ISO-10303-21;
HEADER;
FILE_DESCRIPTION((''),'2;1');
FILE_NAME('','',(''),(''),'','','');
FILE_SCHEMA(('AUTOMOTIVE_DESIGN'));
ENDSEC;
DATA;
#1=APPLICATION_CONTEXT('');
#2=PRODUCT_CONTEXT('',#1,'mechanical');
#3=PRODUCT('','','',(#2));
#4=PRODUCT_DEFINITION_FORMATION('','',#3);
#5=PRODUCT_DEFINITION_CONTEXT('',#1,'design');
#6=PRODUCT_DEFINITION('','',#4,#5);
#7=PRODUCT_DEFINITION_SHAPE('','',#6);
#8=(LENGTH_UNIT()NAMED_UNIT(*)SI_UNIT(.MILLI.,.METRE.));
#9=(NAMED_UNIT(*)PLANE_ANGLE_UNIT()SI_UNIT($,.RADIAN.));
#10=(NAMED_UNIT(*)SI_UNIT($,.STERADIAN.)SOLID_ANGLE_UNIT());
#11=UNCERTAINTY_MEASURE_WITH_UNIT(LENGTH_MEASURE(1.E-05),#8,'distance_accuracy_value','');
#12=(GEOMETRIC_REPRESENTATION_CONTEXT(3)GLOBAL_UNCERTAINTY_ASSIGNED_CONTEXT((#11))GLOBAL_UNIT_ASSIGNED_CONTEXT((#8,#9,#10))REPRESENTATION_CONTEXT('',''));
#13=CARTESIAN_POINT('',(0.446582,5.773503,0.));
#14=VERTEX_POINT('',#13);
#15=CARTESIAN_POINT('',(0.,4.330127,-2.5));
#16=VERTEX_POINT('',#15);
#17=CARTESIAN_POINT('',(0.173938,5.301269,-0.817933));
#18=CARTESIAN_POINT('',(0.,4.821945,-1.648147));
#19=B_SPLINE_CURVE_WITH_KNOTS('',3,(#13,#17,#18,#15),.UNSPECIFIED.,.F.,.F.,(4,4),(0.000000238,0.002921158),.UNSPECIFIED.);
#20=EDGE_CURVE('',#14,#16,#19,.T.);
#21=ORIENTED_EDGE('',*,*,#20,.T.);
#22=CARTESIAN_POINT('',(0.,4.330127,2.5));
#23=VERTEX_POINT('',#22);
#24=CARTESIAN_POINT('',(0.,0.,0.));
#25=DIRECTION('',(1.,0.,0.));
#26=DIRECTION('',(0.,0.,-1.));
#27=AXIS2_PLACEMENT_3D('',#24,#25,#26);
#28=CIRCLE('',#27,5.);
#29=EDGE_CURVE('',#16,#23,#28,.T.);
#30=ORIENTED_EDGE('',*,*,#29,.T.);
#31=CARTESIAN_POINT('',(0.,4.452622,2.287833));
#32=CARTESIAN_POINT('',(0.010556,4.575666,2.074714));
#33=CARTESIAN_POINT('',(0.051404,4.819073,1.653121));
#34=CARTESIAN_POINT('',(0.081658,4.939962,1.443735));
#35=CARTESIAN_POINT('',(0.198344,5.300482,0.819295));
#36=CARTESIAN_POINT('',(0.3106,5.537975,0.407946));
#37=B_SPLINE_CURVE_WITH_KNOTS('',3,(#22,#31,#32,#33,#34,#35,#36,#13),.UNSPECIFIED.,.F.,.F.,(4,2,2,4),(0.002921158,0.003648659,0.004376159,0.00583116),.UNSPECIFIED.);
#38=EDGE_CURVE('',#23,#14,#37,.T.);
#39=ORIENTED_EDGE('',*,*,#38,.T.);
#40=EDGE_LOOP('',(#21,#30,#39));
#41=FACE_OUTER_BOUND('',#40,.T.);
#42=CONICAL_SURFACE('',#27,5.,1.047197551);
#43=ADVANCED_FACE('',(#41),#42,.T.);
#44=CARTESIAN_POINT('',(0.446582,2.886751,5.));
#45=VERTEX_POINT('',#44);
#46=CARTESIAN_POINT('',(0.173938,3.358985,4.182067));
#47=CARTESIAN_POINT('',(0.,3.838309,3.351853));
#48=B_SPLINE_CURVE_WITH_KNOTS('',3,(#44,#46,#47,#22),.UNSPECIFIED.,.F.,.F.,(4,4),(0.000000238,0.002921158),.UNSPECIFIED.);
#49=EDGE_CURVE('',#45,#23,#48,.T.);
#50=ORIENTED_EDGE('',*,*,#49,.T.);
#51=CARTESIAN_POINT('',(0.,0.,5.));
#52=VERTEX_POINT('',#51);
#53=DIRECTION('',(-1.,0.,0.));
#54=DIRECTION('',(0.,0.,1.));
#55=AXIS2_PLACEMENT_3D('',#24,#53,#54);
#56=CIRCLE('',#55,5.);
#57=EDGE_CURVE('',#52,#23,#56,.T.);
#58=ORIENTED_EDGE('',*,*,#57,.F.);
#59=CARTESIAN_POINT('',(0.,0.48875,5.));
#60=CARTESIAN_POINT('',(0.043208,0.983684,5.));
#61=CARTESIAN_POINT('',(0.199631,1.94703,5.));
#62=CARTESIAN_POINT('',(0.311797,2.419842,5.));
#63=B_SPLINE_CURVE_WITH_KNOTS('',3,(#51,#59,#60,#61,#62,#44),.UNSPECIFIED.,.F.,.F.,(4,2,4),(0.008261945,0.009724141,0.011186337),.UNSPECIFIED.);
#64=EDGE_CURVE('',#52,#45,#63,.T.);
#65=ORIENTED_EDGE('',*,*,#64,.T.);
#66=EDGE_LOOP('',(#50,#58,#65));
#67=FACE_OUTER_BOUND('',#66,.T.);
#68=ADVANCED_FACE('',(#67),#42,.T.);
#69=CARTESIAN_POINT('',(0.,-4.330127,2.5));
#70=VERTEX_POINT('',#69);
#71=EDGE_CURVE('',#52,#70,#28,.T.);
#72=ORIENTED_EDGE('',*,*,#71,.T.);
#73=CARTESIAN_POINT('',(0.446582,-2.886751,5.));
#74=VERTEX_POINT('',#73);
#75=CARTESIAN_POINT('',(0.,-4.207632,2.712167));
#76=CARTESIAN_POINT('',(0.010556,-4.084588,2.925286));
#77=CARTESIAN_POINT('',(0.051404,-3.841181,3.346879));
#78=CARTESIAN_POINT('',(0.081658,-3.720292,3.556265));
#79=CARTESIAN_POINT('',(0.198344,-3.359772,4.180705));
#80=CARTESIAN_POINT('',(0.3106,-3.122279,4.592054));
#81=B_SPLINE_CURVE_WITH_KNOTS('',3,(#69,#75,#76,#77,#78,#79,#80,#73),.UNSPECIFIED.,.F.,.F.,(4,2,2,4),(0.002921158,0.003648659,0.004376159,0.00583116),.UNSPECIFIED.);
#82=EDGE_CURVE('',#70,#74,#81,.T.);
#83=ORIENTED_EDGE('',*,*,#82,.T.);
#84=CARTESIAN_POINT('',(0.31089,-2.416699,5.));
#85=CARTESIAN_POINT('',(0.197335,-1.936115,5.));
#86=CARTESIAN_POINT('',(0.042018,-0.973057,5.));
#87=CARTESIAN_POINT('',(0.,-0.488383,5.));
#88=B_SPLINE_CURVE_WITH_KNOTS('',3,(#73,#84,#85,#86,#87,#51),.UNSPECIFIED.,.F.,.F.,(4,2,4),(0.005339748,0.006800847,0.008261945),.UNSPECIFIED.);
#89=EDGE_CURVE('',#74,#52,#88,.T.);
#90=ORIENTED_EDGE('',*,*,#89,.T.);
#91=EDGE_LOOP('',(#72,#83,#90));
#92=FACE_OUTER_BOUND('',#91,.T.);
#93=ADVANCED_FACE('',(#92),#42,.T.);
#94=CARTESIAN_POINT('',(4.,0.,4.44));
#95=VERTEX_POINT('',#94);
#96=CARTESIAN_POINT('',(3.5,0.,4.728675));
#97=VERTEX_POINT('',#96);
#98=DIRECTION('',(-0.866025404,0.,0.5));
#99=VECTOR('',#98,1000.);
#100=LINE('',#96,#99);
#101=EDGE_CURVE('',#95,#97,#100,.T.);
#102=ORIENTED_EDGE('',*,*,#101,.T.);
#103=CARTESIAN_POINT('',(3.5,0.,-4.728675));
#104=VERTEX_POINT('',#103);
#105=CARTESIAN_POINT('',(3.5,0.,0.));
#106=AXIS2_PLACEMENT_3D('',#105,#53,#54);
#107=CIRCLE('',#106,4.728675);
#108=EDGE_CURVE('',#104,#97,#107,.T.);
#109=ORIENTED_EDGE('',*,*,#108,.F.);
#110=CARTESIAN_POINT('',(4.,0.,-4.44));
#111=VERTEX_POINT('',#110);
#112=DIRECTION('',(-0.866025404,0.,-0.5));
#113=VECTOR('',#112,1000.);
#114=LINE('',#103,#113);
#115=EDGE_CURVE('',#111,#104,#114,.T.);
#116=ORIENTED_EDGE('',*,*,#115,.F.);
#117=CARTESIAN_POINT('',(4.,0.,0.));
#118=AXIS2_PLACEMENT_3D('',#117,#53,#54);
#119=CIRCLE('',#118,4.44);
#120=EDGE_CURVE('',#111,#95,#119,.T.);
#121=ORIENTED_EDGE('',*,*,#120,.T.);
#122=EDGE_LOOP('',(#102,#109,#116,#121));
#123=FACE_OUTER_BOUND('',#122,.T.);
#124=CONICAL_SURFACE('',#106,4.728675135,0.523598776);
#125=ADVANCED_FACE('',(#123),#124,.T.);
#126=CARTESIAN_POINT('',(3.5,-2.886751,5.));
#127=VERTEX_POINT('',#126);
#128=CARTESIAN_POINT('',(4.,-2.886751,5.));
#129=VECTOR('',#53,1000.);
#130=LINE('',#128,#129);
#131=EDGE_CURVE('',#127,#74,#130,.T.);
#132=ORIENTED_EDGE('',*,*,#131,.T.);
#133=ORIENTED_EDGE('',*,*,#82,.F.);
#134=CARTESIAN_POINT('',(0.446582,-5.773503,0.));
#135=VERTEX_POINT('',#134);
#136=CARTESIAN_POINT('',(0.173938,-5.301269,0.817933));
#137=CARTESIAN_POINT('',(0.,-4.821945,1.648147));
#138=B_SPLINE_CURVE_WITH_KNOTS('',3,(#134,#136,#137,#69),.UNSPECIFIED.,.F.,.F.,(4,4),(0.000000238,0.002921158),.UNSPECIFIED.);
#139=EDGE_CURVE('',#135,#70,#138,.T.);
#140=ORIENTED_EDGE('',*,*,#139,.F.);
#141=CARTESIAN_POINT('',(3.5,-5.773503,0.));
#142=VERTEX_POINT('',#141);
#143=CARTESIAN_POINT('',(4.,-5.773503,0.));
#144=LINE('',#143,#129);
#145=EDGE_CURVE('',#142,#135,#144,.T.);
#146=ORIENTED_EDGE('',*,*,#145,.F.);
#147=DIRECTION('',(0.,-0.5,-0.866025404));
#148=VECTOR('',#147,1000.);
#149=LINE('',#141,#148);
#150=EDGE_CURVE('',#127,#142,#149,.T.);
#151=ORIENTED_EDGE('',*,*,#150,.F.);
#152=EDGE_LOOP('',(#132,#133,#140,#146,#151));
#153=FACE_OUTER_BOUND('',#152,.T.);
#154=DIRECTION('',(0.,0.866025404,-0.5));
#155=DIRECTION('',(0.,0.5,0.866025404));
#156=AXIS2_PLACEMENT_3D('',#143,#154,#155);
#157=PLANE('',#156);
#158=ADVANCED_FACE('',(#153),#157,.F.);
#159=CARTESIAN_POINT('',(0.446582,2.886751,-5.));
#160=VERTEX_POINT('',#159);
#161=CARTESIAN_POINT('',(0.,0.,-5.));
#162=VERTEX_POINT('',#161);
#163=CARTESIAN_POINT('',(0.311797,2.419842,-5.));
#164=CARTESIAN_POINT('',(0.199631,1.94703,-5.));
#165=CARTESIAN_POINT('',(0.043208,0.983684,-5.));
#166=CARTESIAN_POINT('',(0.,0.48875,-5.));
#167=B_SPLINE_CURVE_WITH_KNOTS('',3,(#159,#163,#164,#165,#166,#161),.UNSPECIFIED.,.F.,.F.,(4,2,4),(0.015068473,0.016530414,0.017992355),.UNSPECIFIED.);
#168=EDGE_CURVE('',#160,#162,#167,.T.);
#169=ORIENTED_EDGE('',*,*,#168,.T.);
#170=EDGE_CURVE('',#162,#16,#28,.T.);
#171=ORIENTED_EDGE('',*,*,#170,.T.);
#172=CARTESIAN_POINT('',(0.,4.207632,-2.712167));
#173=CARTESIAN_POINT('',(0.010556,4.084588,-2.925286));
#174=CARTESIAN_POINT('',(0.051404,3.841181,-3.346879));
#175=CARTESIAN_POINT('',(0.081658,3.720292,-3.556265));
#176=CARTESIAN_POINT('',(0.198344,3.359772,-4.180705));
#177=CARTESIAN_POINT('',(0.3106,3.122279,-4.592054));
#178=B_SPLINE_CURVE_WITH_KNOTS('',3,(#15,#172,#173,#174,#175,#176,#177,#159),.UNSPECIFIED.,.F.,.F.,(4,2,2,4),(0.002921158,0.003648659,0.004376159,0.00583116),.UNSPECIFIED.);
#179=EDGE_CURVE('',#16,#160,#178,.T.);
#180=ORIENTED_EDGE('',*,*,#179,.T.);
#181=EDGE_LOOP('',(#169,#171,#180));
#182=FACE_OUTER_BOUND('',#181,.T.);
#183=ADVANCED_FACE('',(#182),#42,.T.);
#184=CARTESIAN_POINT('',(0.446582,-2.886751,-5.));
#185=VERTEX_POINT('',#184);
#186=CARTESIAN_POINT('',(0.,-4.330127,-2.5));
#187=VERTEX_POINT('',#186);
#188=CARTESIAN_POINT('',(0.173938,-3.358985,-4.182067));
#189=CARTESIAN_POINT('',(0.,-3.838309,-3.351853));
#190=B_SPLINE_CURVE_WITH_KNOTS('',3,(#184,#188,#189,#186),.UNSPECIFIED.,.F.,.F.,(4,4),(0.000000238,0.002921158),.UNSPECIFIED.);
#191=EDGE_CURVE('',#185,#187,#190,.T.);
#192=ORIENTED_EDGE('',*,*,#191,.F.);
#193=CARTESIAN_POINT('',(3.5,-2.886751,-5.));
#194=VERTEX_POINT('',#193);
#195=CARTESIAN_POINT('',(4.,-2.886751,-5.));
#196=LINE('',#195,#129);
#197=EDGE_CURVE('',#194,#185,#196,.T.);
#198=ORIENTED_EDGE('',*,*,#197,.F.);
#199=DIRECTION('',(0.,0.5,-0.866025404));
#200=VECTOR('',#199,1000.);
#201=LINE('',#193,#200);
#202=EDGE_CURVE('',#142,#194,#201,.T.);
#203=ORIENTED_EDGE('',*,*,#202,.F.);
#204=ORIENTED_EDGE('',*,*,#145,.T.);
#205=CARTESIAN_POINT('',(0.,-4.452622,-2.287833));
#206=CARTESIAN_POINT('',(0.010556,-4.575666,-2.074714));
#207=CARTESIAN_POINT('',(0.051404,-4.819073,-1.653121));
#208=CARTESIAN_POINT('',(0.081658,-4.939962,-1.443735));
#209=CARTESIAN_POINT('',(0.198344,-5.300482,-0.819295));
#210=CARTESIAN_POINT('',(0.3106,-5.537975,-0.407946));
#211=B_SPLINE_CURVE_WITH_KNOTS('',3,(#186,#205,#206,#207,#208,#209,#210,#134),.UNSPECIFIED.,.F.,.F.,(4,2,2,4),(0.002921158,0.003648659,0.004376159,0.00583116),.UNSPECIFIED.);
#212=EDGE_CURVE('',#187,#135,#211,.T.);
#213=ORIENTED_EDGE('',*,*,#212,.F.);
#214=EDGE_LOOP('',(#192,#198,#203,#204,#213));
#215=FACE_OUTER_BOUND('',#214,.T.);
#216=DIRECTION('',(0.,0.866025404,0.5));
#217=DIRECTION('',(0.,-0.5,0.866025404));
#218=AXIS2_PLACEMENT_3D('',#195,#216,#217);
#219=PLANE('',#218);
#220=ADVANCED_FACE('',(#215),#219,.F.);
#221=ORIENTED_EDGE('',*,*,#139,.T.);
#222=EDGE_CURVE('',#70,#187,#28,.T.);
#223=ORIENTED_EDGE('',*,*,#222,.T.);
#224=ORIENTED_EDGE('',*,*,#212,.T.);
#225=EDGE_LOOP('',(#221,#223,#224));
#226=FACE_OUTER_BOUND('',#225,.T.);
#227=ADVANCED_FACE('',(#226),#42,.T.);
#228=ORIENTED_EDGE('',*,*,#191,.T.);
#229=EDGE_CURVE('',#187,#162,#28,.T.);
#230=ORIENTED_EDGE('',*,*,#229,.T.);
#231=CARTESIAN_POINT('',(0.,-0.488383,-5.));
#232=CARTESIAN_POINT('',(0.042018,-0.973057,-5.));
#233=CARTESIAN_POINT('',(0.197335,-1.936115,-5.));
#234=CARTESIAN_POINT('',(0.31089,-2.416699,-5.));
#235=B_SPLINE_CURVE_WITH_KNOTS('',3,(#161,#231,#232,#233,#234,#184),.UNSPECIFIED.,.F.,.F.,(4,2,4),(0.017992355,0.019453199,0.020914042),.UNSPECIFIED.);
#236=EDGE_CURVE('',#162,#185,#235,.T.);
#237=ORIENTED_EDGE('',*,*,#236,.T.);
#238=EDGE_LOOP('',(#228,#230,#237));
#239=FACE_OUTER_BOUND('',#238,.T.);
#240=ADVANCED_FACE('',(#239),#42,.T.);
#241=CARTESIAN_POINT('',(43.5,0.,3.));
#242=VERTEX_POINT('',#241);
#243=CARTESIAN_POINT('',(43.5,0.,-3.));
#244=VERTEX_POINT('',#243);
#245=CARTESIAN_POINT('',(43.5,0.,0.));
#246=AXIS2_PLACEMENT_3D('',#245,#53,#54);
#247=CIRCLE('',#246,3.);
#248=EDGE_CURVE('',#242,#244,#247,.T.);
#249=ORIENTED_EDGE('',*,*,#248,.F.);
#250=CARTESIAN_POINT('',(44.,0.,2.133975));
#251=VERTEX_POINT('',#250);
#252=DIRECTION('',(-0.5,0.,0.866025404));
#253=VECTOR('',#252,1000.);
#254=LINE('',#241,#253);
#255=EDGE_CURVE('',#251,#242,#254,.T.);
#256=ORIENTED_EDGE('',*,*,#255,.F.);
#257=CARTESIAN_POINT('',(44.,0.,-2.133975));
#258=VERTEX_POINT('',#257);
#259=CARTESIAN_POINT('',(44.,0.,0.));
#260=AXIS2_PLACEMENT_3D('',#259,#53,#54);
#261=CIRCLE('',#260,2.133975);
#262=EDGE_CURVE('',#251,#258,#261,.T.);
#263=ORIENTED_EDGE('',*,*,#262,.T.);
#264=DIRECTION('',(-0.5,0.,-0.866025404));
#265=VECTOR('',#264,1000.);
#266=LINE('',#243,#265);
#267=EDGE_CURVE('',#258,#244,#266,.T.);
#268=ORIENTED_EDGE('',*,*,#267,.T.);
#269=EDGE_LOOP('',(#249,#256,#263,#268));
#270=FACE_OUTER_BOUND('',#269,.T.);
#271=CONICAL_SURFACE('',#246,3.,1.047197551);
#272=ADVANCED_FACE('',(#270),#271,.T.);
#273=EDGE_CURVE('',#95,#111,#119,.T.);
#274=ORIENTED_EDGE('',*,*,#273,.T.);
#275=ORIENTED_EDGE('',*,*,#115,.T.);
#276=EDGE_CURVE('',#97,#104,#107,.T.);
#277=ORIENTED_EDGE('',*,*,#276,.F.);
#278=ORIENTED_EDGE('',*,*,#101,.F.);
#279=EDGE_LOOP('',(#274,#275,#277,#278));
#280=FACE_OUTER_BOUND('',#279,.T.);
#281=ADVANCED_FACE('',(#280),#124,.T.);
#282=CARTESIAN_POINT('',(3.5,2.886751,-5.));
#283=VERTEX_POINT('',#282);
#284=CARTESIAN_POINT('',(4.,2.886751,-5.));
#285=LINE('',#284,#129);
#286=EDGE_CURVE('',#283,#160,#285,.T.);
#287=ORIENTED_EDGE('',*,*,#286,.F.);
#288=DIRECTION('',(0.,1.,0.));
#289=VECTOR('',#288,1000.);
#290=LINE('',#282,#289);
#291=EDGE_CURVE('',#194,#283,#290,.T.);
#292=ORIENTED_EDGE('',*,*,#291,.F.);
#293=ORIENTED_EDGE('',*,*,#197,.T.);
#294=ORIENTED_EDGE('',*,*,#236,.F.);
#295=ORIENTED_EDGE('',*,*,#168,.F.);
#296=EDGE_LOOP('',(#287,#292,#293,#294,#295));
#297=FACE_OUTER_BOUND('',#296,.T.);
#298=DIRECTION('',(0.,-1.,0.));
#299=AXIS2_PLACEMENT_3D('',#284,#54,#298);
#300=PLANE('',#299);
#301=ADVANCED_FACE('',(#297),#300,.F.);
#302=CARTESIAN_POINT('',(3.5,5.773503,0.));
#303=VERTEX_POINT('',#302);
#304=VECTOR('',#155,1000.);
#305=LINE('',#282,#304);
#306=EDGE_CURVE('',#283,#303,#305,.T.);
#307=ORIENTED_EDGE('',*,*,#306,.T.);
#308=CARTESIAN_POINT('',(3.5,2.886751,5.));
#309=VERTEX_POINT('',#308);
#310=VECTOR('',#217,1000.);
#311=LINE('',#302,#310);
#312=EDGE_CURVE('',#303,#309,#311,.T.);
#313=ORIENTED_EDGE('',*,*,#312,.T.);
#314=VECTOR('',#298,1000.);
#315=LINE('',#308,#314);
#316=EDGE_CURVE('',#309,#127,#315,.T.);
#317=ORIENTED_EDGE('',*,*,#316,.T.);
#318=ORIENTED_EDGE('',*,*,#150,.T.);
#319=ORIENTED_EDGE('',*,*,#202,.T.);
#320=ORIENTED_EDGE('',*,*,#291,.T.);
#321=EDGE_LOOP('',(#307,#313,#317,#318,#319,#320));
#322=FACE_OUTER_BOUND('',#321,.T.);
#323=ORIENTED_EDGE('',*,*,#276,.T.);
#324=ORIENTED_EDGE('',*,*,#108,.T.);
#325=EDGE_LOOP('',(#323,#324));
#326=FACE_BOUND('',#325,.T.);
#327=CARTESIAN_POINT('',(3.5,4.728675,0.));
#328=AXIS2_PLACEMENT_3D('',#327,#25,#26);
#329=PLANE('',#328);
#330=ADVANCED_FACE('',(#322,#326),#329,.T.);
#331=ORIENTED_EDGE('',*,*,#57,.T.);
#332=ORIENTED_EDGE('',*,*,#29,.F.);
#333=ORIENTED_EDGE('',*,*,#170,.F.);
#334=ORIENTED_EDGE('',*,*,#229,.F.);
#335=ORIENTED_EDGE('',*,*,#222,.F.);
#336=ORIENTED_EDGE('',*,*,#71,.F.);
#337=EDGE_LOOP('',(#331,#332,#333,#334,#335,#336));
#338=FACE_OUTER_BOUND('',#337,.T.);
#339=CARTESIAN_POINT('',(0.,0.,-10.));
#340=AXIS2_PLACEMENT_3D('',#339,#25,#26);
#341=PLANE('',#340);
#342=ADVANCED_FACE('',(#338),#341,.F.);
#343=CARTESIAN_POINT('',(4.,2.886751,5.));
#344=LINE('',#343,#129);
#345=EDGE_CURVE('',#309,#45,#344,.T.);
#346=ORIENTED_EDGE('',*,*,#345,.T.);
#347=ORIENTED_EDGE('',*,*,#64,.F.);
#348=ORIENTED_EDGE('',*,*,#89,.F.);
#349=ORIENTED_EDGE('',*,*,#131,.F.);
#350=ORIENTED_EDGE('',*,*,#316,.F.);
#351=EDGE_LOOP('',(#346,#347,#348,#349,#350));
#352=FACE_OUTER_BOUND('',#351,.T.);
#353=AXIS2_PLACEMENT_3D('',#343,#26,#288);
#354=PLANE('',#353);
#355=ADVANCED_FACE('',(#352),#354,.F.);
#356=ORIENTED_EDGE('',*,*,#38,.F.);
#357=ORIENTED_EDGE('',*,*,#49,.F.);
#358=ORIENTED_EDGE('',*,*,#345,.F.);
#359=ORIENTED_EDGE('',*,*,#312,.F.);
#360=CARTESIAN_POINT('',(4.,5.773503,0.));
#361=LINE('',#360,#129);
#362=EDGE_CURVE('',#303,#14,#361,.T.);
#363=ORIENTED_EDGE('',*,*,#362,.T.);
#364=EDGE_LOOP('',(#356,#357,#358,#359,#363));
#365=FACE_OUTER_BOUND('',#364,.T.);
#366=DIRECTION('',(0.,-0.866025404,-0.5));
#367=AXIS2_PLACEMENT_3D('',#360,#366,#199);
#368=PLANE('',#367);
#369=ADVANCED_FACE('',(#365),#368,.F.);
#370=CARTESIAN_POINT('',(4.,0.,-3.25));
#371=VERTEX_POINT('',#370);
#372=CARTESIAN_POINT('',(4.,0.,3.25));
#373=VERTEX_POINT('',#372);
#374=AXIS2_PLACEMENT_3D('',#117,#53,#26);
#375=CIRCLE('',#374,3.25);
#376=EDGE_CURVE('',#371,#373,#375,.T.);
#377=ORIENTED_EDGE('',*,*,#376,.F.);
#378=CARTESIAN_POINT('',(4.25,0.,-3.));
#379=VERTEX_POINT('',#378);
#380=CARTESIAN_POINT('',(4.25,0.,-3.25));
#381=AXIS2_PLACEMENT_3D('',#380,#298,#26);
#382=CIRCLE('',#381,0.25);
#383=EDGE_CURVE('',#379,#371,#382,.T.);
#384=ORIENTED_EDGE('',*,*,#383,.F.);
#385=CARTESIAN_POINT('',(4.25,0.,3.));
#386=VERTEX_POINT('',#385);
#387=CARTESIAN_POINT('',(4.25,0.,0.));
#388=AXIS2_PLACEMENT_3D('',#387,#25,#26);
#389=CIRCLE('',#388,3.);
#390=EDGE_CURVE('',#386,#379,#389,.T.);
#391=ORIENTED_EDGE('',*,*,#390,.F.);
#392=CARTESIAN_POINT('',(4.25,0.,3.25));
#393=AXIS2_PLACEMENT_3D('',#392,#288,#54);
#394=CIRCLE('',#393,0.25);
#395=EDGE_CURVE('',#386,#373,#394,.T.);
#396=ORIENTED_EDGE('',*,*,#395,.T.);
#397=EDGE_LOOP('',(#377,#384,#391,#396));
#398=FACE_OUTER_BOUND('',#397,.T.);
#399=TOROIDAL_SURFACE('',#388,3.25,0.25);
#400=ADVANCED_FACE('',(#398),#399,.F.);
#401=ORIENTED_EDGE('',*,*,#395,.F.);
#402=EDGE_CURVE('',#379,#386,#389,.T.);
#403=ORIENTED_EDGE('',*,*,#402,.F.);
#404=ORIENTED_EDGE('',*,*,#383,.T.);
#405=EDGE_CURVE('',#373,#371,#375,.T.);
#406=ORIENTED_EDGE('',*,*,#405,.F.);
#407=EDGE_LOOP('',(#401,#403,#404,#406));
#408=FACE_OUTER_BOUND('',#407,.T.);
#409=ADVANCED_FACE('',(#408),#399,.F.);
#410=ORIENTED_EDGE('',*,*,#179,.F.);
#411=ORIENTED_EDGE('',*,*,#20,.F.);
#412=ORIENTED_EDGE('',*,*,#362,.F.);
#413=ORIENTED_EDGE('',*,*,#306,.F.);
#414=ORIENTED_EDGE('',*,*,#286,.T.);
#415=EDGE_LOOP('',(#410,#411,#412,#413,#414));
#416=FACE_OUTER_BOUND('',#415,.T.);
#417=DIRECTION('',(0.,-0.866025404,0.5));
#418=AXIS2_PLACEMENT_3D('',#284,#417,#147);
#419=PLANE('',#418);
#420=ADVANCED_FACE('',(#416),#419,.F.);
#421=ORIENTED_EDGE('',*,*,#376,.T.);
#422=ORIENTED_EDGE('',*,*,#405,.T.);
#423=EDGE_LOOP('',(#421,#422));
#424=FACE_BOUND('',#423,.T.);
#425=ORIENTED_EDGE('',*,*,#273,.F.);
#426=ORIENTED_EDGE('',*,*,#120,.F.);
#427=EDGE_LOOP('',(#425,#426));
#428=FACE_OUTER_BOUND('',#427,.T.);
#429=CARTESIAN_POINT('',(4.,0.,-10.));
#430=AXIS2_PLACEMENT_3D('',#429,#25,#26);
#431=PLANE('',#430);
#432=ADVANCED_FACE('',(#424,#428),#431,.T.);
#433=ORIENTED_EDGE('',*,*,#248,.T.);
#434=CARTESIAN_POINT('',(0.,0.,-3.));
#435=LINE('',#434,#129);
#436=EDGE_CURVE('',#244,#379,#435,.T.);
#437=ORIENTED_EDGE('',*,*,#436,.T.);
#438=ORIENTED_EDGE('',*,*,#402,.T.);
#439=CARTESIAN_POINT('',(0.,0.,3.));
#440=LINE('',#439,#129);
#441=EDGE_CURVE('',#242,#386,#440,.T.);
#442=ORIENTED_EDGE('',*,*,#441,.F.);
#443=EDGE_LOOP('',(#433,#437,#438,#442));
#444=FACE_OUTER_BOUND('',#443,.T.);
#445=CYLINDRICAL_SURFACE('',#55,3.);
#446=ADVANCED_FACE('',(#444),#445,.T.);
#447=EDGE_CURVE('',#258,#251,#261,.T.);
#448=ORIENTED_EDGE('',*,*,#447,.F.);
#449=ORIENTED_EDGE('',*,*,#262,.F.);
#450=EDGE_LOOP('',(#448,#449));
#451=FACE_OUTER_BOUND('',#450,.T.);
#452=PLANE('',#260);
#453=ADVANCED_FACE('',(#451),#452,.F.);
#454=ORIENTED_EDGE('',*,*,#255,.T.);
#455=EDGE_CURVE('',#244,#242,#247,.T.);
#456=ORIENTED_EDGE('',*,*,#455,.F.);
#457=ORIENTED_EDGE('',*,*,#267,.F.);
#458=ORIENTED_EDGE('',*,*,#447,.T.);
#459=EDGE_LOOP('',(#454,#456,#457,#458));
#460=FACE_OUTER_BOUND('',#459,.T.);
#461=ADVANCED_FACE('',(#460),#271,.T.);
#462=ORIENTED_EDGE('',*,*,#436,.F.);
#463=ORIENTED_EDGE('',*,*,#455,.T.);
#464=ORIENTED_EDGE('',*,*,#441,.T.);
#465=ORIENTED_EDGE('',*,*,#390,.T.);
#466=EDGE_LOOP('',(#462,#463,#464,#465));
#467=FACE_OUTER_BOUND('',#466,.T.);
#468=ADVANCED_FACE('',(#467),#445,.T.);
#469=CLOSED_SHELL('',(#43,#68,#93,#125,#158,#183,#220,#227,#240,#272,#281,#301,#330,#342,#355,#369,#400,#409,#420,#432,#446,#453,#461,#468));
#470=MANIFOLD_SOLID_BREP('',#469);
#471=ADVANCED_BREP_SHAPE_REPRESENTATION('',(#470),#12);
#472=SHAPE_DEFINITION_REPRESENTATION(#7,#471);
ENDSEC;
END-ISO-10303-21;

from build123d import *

# Parameters (mm, degrees)
EXTRUDE_390_DEPTH = 4
FILLET_1290_R     = 0.25


with BuildPart() as part:
    # 草图1 → Extrude 390 (new body)
    with BuildSketch(Plane(origin=(0, 0, 0), x_dir=(0, 0, -1), z_dir=(1, 0, 0))):
        Polygon((5, 2.886751346), (5, -2.886751346), (0, -5.773502692), (-5, -2.886751346), (-5, 2.886751346), (0, 5.773502692), align=None)
    extrude(amount=EXTRUDE_390_DEPTH)

    # 草图2 → 凸台-旋转1 (revolve)
    with BuildSketch(Plane.XY, mode=Mode.PRIVATE) as revolve_1_sk:
        Polygon((0, 0), (44, 0), (44, 2.134), (44, 3), (0, 3), align=None)
    revolve(revolve_1_sk.sketch.rotate(Axis((0, 0, 0), (1, 0, 0)), 90), axis=Axis((0, 0, 0), (1, 0, 0)))

    # 草图3 → 切除-旋转1 (revolve, cut)
    with BuildSketch(Plane.XY):
        Polygon((0, 5), (3.333333333, 10.773502692), (3.333333333, 15.773502692), (-10, 15.773502692), (-10, 5), align=None)
    revolve(axis=Axis((0, 0, 0), (1, 0, 0)), mode=Mode.SUBTRACT)

    # 草图4 → 切除-旋转3 (revolve, cut)
    with BuildSketch(Plane.XY, mode=Mode.PRIVATE) as cut_revolve_3_sk:
        Polygon((4, 4.44), (3.5, 4.728675135), (3.5, 5.773502692), (4, 5.773502692), align=None)
    revolve(cut_revolve_3_sk.sketch.rotate(Axis((0, 0, 0), (1, 0, 0)), 90), axis=Axis((0, 0, 0), (1, 0, 0)), mode=Mode.SUBTRACT)

    # Fillet 1290
    fillet_1290_edges = [part.edges().sort_by_distance(p)[0] for p in [
        (4, 0, -3),
    ]]
    fillet(fillet_1290_edges, radius=FILLET_1290_R)

    # 草图6 → 切除-旋转4 (revolve, cut)
    with BuildSketch(Plane.XY, mode=Mode.PRIVATE) as cut_revolve_4_sk:
        Polygon((43.5, 3), (44.5, 3), (44, 2.133974596), align=None)
    revolve(cut_revolve_4_sk.sketch.rotate(Axis((0, 0, 0), (1, 0, 0)), 90), axis=Axis((0, 0, 0), (1, 0, 0)), mode=Mode.SUBTRACT)


solid = part.part
